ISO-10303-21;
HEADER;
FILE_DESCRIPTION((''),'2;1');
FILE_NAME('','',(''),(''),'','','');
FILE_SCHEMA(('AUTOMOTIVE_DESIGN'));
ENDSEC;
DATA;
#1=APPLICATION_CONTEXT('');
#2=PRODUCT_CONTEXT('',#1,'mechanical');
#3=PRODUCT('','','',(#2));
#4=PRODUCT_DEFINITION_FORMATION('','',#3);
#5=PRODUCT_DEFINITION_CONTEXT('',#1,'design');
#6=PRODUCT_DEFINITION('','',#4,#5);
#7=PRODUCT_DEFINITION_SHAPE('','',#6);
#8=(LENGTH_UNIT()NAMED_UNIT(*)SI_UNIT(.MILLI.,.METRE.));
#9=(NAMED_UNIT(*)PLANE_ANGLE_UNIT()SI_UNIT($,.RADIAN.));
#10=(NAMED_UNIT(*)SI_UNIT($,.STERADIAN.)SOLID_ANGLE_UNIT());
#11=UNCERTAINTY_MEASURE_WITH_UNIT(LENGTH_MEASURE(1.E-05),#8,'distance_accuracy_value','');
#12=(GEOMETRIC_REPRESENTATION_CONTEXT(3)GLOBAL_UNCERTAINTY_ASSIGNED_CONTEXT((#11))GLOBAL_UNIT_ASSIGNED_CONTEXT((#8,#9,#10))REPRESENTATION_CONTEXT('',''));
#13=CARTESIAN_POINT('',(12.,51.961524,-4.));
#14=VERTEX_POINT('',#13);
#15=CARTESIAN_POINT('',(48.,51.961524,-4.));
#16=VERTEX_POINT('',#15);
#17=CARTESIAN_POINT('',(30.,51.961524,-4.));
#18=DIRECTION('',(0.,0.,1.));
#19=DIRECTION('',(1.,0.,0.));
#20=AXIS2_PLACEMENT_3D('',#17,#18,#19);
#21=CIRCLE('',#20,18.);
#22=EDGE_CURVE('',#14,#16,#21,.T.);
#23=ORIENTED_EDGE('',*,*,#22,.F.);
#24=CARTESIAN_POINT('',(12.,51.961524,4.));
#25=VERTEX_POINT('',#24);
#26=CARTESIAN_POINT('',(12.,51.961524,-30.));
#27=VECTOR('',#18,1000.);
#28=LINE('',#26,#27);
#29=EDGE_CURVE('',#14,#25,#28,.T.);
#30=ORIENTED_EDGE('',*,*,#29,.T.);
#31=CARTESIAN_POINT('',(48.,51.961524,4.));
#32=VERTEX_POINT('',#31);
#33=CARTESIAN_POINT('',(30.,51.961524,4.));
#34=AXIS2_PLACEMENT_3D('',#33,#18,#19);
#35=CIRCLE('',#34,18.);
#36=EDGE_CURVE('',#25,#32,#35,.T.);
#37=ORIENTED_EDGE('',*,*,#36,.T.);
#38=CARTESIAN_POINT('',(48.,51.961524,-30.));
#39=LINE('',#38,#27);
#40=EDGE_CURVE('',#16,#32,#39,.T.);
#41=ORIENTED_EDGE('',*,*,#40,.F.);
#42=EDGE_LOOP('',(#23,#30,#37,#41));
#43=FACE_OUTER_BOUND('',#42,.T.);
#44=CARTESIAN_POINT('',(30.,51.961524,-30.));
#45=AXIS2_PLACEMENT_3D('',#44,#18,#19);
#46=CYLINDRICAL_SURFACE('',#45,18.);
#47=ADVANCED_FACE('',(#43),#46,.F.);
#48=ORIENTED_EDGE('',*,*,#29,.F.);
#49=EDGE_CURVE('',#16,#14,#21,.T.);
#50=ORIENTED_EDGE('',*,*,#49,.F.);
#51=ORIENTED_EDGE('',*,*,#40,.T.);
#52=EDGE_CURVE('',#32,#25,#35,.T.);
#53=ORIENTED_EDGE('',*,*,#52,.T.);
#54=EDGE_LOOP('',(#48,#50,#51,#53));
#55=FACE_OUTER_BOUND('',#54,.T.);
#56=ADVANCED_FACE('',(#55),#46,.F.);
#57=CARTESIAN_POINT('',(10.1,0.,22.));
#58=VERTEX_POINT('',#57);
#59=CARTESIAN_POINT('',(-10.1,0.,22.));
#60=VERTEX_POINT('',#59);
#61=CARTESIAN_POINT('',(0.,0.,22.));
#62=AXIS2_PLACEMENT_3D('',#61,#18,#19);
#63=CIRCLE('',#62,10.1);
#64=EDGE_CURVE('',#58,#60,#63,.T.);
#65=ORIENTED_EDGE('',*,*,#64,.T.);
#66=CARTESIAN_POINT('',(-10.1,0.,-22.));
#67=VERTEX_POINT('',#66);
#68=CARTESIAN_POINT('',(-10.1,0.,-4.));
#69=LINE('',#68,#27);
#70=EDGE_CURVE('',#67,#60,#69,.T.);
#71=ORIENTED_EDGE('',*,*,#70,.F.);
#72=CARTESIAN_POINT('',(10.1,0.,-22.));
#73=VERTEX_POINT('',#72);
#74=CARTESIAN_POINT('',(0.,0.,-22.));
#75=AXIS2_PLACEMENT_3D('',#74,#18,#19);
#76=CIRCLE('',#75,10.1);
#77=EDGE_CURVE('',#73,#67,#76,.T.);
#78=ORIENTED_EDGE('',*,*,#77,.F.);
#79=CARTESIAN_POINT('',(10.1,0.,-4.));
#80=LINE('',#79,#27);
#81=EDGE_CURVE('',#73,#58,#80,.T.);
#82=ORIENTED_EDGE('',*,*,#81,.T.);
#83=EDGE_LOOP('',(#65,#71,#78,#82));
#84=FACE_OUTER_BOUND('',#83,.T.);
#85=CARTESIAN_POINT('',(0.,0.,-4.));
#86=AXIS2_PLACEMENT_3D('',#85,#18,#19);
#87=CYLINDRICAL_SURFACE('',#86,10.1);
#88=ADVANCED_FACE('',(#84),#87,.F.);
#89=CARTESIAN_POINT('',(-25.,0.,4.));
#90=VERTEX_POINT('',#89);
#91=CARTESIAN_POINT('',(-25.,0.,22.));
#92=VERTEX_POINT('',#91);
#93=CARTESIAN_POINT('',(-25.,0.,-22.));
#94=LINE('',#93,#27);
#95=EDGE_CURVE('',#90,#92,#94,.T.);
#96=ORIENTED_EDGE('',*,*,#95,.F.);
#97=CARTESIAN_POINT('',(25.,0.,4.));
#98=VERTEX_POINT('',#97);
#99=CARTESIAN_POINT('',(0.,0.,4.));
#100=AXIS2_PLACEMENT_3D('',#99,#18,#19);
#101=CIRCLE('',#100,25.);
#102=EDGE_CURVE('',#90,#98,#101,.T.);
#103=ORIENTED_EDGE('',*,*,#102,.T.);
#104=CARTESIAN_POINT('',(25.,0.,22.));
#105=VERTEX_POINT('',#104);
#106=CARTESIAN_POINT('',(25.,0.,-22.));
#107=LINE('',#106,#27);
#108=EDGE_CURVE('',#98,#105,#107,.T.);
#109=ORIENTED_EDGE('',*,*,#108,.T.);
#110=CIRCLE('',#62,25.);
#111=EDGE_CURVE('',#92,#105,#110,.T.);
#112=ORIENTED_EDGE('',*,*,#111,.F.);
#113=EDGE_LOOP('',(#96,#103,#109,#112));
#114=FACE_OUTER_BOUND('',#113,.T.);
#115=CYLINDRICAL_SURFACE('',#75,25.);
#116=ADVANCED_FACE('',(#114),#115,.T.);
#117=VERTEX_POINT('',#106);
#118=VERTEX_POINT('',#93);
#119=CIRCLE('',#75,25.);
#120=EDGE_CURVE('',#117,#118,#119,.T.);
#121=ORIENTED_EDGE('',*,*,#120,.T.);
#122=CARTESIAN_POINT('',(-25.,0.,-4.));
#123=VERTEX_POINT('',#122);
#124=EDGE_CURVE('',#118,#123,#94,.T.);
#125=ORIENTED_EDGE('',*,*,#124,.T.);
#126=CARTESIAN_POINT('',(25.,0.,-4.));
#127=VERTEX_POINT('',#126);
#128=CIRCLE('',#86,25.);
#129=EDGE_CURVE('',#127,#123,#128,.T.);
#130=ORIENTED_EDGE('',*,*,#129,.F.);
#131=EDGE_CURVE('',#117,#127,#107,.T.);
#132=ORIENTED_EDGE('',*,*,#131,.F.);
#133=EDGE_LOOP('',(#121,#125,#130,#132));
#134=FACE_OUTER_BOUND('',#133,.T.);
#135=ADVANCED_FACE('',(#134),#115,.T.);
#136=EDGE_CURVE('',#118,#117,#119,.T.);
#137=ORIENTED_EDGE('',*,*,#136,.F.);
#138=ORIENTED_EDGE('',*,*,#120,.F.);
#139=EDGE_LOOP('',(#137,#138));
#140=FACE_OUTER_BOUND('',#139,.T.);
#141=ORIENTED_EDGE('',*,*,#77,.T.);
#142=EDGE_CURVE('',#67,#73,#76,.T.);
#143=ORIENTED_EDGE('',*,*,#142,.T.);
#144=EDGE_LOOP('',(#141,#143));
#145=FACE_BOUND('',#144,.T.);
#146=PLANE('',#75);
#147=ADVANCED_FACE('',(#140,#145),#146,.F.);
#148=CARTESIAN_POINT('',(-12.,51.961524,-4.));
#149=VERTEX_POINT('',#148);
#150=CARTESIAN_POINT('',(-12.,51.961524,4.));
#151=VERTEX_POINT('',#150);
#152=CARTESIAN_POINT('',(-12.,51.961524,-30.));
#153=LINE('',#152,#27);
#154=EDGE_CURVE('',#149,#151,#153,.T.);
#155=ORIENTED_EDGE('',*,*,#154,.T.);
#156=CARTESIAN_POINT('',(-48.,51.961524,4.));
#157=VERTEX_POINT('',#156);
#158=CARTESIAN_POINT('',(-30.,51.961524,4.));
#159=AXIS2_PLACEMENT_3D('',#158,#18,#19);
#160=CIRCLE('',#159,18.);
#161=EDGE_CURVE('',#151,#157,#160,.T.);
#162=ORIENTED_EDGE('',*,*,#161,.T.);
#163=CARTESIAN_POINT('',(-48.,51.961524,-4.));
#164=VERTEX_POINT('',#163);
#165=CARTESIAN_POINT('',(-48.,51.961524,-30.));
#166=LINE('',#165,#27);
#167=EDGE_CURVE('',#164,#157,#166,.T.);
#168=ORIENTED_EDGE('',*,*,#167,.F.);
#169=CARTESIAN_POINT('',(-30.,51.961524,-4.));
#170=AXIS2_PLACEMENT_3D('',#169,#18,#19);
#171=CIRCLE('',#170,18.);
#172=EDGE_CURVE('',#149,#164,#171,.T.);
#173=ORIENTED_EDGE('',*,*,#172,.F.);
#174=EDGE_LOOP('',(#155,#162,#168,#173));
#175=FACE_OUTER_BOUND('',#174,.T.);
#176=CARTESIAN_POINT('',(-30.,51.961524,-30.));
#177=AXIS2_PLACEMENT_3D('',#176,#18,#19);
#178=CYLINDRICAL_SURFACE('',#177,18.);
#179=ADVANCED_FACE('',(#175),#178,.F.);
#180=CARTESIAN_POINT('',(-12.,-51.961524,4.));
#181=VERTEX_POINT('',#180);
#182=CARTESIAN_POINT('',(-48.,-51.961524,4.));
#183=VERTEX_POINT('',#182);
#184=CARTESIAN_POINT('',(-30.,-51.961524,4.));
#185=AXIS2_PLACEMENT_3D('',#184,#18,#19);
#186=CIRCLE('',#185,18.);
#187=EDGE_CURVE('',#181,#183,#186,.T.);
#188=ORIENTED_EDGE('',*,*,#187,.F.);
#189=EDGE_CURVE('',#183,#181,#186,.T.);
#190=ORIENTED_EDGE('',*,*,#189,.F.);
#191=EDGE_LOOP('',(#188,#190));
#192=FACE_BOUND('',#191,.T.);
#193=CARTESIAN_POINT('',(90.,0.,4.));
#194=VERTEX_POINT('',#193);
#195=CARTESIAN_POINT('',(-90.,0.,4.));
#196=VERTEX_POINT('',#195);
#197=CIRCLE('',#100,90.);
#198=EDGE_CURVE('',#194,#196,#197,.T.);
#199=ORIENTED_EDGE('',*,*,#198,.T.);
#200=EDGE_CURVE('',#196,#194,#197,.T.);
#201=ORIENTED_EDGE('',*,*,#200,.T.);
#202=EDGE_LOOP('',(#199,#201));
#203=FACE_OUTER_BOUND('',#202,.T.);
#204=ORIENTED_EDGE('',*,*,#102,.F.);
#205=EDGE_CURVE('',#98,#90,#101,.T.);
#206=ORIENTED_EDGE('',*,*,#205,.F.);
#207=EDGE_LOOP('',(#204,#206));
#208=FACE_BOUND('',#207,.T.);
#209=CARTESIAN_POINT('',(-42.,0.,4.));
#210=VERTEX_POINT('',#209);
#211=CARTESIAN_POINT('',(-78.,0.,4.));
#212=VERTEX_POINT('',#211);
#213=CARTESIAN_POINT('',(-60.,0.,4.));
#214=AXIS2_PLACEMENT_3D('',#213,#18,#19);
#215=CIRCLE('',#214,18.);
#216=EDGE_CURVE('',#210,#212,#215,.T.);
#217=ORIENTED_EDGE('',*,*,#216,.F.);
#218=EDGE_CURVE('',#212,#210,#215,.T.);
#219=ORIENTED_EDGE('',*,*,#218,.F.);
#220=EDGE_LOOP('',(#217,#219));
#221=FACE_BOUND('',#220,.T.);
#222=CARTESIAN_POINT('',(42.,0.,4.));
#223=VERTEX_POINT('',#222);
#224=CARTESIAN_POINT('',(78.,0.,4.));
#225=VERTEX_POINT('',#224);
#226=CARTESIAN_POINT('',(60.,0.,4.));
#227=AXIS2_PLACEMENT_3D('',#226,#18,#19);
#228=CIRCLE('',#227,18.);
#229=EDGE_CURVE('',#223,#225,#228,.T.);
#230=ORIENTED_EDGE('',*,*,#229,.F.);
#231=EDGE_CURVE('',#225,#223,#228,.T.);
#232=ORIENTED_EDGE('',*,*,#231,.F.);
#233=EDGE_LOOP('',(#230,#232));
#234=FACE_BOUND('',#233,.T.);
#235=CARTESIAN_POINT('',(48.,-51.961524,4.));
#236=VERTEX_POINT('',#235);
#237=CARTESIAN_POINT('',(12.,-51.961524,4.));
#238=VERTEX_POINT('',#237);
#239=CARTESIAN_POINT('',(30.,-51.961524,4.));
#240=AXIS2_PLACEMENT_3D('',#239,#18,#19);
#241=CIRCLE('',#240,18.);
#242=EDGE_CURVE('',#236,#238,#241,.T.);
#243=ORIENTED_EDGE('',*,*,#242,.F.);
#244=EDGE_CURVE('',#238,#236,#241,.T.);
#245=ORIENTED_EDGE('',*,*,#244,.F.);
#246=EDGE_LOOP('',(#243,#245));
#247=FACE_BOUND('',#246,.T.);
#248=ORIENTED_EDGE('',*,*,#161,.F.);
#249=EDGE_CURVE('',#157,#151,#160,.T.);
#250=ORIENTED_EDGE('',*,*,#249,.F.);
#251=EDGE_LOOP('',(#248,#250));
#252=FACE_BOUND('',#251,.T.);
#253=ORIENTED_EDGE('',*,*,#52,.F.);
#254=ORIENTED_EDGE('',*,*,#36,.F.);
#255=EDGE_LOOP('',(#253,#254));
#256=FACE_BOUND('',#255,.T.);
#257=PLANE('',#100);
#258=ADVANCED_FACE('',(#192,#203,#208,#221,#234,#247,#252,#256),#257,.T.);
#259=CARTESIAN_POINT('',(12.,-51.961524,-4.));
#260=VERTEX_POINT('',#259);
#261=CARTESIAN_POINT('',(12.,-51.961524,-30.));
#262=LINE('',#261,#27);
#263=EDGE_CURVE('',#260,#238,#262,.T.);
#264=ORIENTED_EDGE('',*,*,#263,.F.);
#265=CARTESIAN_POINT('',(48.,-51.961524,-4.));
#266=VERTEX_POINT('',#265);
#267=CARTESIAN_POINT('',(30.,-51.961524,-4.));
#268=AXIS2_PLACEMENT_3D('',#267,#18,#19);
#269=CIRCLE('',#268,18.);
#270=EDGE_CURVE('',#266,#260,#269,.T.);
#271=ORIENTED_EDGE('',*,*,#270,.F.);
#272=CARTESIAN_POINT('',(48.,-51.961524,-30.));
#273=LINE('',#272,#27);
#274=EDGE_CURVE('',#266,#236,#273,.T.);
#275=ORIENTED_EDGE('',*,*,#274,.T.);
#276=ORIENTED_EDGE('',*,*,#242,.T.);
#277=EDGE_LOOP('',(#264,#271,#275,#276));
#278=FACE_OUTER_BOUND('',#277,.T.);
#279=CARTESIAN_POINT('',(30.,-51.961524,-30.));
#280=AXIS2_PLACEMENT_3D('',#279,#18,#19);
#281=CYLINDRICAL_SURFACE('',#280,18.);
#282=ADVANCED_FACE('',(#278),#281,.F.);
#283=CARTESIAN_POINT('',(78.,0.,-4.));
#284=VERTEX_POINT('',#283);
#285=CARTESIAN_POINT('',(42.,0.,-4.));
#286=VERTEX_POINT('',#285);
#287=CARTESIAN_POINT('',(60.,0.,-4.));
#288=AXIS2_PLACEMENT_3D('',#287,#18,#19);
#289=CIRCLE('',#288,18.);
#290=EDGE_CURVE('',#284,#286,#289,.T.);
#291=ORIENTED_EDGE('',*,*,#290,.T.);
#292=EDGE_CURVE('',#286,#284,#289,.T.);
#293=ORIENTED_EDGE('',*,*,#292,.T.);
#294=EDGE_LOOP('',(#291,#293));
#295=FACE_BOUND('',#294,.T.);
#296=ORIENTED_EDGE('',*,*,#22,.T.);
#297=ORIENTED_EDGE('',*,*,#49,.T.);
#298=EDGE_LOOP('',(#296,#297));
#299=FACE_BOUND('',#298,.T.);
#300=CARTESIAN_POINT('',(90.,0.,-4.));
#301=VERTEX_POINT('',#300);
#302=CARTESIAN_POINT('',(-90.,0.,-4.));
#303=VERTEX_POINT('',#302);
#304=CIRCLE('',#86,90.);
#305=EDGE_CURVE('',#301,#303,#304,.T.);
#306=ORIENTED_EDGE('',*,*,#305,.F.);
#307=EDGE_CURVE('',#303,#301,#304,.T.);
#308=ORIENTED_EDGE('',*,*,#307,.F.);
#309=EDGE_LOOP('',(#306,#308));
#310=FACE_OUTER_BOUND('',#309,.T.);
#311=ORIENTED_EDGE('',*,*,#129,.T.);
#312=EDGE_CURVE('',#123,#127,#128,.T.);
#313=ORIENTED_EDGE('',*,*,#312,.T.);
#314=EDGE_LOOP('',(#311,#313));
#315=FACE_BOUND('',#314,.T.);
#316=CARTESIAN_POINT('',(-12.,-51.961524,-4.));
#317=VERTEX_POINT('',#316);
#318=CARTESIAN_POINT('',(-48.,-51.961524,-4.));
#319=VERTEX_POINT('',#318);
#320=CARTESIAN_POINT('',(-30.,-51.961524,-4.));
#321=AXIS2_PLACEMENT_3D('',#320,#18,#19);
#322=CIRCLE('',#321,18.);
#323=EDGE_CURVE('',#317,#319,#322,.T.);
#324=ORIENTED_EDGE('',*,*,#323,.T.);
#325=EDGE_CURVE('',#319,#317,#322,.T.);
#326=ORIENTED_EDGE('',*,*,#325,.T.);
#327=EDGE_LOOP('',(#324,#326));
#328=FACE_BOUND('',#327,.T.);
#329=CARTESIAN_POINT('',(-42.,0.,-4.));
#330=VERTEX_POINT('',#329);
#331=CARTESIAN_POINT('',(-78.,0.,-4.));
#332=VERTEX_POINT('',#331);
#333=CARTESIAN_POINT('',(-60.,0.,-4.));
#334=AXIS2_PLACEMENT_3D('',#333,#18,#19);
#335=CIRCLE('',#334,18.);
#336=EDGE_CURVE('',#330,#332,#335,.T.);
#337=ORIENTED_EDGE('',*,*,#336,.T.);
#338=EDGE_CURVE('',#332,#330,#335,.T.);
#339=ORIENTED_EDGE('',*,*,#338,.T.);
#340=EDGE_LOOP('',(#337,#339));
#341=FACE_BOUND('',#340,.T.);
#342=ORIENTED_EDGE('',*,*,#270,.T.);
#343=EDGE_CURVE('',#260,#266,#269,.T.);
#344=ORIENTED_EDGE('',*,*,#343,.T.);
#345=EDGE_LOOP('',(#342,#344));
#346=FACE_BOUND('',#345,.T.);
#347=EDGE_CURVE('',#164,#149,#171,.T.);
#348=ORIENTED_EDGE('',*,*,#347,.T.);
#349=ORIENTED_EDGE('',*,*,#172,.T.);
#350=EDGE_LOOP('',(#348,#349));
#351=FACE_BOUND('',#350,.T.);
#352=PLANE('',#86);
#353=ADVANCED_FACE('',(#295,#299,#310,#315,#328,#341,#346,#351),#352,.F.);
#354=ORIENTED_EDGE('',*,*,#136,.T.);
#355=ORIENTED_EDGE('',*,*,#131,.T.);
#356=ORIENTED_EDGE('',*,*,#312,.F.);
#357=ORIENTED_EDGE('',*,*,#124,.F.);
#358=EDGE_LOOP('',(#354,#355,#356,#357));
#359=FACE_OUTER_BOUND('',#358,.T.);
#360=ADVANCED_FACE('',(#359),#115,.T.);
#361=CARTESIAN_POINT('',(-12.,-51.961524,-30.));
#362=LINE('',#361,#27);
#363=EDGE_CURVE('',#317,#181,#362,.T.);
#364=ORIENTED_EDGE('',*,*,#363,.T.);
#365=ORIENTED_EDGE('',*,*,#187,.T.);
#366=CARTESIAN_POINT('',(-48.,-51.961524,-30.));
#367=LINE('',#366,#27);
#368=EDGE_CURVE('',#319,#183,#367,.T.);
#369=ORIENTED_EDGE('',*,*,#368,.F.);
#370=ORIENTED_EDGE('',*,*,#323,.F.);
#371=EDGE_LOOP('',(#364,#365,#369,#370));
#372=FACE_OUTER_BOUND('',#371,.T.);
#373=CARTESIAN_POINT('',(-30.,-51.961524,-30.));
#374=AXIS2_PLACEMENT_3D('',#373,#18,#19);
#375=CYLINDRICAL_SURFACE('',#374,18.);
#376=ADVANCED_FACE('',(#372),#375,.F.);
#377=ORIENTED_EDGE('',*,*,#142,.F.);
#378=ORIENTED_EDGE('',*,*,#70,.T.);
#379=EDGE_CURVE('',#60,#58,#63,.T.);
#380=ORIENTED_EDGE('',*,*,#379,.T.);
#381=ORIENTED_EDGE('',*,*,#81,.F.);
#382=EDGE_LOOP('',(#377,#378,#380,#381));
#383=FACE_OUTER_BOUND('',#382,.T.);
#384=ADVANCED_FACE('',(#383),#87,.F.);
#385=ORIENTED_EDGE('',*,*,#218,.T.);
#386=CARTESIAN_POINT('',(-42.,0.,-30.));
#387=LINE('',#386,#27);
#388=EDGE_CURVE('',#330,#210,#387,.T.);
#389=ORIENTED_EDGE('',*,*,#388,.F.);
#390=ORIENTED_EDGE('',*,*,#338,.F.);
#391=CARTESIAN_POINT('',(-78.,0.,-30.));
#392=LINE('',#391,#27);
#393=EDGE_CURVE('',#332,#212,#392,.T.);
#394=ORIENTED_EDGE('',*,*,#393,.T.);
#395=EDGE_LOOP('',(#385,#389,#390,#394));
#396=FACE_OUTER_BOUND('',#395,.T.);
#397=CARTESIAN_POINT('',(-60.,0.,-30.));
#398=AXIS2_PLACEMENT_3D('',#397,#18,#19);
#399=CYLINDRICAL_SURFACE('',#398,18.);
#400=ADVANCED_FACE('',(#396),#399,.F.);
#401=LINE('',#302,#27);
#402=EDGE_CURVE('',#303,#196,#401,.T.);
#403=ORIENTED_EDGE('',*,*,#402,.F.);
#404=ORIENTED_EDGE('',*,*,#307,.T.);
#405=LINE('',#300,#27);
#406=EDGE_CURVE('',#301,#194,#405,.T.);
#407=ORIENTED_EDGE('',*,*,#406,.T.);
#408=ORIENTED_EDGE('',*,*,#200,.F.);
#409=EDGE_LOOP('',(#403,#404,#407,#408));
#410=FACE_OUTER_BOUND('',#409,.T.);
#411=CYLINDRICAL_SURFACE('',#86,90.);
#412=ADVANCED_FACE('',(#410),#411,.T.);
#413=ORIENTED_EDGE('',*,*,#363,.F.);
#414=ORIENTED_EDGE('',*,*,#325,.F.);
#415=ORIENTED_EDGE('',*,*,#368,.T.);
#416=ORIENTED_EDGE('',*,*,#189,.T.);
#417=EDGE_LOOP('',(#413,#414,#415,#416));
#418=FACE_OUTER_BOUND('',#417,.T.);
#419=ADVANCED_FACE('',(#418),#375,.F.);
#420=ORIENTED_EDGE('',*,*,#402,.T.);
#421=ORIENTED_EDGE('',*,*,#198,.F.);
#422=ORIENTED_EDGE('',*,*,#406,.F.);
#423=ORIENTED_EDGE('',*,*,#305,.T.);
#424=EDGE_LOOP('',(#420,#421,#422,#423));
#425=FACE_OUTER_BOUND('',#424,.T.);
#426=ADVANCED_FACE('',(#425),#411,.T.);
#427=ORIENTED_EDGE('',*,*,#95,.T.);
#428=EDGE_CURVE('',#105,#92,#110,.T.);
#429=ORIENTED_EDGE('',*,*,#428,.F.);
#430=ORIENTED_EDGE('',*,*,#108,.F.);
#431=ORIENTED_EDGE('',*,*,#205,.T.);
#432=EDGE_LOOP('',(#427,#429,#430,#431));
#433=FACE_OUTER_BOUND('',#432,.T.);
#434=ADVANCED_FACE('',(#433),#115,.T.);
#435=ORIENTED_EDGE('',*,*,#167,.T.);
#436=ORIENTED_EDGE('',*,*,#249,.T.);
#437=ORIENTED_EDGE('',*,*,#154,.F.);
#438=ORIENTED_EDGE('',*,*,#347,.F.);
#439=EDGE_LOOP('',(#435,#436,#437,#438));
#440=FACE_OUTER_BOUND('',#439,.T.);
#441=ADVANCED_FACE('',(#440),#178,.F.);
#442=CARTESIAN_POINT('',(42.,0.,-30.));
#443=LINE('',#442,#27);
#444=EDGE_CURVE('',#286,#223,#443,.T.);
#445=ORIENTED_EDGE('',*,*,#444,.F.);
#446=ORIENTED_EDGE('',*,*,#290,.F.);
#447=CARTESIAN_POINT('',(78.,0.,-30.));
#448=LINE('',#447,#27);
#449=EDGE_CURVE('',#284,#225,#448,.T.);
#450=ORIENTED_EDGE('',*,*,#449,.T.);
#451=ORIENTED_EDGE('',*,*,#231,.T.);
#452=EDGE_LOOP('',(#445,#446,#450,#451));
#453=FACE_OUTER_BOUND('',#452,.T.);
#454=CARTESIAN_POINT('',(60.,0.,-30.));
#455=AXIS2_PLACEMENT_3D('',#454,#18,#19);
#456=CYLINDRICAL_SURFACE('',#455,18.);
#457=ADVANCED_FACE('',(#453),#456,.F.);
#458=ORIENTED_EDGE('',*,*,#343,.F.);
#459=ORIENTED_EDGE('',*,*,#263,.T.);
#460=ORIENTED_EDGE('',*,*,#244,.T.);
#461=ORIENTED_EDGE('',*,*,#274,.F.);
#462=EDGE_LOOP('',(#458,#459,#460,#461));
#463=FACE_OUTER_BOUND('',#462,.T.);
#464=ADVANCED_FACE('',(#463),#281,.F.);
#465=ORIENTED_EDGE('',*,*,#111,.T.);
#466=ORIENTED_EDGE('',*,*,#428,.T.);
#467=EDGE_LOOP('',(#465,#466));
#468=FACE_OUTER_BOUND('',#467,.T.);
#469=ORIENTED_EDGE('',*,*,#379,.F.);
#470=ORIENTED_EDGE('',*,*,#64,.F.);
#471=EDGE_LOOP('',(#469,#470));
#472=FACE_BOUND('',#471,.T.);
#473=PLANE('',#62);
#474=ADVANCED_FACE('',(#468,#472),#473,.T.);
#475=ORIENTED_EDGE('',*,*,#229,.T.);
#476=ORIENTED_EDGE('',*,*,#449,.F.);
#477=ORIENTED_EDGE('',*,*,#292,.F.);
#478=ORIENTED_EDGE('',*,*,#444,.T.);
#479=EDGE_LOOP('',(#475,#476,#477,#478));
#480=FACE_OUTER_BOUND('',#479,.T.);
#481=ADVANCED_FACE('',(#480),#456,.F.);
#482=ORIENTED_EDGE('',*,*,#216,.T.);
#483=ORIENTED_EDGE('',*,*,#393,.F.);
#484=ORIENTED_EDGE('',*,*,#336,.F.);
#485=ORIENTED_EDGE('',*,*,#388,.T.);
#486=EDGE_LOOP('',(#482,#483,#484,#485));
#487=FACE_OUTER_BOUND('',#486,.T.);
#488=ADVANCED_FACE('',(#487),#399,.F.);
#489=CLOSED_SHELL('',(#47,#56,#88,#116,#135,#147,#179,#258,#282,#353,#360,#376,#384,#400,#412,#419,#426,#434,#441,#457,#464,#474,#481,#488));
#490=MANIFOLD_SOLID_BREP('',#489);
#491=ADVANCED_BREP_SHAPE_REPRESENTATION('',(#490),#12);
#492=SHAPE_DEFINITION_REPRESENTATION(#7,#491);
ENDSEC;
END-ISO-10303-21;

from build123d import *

# Parameters (mm, degrees)
SKETCH_1_R          = 90
SKETCH_1_R_2        = 10.1
EXTRUDE_1_DEPTH     = 4
SKETCH_2_R          = 25
SKETCH_2_R_2        = 10.1
EXTRUDE_2_DEPTH     = 22
SKETCH_3_R          = 18
CUT_EXTRUDE_1_DEPTH = 30


with BuildPart() as part:
    # 草图1 → 凸台-拉伸1 (new, symmetric)
    with BuildSketch(Plane.XY):
        Circle(SKETCH_1_R)
        Circle(SKETCH_1_R_2, mode=Mode.SUBTRACT)
    extrude(amount=EXTRUDE_1_DEPTH, both=True)

    # 草图2 → 凸台-拉伸2 (add, symmetric)
    with BuildSketch(Plane.XY):
        Circle(SKETCH_2_R)
        Circle(SKETCH_2_R_2, mode=Mode.SUBTRACT)
    extrude(amount=EXTRUDE_2_DEPTH, both=True)

    # 草图3 → 切除-拉伸1 (cut, symmetric)
    with BuildSketch(Plane.XY):
        with Locations((60, 0)):
            Circle(SKETCH_3_R)
        with Locations((30, 51.961524227)):
            Circle(SKETCH_3_R)
        with Locations((-30, 51.961524227)):
            Circle(SKETCH_3_R)
        with Locations((-60, 0)):
            Circle(SKETCH_3_R)
        with Locations((-30, -51.961524227)):
            Circle(SKETCH_3_R)
        with Locations((30, -51.961524227)):
            Circle(SKETCH_3_R)
    extrude(amount=CUT_EXTRUDE_1_DEPTH, both=True, mode=Mode.SUBTRACT)


solid = part.part
